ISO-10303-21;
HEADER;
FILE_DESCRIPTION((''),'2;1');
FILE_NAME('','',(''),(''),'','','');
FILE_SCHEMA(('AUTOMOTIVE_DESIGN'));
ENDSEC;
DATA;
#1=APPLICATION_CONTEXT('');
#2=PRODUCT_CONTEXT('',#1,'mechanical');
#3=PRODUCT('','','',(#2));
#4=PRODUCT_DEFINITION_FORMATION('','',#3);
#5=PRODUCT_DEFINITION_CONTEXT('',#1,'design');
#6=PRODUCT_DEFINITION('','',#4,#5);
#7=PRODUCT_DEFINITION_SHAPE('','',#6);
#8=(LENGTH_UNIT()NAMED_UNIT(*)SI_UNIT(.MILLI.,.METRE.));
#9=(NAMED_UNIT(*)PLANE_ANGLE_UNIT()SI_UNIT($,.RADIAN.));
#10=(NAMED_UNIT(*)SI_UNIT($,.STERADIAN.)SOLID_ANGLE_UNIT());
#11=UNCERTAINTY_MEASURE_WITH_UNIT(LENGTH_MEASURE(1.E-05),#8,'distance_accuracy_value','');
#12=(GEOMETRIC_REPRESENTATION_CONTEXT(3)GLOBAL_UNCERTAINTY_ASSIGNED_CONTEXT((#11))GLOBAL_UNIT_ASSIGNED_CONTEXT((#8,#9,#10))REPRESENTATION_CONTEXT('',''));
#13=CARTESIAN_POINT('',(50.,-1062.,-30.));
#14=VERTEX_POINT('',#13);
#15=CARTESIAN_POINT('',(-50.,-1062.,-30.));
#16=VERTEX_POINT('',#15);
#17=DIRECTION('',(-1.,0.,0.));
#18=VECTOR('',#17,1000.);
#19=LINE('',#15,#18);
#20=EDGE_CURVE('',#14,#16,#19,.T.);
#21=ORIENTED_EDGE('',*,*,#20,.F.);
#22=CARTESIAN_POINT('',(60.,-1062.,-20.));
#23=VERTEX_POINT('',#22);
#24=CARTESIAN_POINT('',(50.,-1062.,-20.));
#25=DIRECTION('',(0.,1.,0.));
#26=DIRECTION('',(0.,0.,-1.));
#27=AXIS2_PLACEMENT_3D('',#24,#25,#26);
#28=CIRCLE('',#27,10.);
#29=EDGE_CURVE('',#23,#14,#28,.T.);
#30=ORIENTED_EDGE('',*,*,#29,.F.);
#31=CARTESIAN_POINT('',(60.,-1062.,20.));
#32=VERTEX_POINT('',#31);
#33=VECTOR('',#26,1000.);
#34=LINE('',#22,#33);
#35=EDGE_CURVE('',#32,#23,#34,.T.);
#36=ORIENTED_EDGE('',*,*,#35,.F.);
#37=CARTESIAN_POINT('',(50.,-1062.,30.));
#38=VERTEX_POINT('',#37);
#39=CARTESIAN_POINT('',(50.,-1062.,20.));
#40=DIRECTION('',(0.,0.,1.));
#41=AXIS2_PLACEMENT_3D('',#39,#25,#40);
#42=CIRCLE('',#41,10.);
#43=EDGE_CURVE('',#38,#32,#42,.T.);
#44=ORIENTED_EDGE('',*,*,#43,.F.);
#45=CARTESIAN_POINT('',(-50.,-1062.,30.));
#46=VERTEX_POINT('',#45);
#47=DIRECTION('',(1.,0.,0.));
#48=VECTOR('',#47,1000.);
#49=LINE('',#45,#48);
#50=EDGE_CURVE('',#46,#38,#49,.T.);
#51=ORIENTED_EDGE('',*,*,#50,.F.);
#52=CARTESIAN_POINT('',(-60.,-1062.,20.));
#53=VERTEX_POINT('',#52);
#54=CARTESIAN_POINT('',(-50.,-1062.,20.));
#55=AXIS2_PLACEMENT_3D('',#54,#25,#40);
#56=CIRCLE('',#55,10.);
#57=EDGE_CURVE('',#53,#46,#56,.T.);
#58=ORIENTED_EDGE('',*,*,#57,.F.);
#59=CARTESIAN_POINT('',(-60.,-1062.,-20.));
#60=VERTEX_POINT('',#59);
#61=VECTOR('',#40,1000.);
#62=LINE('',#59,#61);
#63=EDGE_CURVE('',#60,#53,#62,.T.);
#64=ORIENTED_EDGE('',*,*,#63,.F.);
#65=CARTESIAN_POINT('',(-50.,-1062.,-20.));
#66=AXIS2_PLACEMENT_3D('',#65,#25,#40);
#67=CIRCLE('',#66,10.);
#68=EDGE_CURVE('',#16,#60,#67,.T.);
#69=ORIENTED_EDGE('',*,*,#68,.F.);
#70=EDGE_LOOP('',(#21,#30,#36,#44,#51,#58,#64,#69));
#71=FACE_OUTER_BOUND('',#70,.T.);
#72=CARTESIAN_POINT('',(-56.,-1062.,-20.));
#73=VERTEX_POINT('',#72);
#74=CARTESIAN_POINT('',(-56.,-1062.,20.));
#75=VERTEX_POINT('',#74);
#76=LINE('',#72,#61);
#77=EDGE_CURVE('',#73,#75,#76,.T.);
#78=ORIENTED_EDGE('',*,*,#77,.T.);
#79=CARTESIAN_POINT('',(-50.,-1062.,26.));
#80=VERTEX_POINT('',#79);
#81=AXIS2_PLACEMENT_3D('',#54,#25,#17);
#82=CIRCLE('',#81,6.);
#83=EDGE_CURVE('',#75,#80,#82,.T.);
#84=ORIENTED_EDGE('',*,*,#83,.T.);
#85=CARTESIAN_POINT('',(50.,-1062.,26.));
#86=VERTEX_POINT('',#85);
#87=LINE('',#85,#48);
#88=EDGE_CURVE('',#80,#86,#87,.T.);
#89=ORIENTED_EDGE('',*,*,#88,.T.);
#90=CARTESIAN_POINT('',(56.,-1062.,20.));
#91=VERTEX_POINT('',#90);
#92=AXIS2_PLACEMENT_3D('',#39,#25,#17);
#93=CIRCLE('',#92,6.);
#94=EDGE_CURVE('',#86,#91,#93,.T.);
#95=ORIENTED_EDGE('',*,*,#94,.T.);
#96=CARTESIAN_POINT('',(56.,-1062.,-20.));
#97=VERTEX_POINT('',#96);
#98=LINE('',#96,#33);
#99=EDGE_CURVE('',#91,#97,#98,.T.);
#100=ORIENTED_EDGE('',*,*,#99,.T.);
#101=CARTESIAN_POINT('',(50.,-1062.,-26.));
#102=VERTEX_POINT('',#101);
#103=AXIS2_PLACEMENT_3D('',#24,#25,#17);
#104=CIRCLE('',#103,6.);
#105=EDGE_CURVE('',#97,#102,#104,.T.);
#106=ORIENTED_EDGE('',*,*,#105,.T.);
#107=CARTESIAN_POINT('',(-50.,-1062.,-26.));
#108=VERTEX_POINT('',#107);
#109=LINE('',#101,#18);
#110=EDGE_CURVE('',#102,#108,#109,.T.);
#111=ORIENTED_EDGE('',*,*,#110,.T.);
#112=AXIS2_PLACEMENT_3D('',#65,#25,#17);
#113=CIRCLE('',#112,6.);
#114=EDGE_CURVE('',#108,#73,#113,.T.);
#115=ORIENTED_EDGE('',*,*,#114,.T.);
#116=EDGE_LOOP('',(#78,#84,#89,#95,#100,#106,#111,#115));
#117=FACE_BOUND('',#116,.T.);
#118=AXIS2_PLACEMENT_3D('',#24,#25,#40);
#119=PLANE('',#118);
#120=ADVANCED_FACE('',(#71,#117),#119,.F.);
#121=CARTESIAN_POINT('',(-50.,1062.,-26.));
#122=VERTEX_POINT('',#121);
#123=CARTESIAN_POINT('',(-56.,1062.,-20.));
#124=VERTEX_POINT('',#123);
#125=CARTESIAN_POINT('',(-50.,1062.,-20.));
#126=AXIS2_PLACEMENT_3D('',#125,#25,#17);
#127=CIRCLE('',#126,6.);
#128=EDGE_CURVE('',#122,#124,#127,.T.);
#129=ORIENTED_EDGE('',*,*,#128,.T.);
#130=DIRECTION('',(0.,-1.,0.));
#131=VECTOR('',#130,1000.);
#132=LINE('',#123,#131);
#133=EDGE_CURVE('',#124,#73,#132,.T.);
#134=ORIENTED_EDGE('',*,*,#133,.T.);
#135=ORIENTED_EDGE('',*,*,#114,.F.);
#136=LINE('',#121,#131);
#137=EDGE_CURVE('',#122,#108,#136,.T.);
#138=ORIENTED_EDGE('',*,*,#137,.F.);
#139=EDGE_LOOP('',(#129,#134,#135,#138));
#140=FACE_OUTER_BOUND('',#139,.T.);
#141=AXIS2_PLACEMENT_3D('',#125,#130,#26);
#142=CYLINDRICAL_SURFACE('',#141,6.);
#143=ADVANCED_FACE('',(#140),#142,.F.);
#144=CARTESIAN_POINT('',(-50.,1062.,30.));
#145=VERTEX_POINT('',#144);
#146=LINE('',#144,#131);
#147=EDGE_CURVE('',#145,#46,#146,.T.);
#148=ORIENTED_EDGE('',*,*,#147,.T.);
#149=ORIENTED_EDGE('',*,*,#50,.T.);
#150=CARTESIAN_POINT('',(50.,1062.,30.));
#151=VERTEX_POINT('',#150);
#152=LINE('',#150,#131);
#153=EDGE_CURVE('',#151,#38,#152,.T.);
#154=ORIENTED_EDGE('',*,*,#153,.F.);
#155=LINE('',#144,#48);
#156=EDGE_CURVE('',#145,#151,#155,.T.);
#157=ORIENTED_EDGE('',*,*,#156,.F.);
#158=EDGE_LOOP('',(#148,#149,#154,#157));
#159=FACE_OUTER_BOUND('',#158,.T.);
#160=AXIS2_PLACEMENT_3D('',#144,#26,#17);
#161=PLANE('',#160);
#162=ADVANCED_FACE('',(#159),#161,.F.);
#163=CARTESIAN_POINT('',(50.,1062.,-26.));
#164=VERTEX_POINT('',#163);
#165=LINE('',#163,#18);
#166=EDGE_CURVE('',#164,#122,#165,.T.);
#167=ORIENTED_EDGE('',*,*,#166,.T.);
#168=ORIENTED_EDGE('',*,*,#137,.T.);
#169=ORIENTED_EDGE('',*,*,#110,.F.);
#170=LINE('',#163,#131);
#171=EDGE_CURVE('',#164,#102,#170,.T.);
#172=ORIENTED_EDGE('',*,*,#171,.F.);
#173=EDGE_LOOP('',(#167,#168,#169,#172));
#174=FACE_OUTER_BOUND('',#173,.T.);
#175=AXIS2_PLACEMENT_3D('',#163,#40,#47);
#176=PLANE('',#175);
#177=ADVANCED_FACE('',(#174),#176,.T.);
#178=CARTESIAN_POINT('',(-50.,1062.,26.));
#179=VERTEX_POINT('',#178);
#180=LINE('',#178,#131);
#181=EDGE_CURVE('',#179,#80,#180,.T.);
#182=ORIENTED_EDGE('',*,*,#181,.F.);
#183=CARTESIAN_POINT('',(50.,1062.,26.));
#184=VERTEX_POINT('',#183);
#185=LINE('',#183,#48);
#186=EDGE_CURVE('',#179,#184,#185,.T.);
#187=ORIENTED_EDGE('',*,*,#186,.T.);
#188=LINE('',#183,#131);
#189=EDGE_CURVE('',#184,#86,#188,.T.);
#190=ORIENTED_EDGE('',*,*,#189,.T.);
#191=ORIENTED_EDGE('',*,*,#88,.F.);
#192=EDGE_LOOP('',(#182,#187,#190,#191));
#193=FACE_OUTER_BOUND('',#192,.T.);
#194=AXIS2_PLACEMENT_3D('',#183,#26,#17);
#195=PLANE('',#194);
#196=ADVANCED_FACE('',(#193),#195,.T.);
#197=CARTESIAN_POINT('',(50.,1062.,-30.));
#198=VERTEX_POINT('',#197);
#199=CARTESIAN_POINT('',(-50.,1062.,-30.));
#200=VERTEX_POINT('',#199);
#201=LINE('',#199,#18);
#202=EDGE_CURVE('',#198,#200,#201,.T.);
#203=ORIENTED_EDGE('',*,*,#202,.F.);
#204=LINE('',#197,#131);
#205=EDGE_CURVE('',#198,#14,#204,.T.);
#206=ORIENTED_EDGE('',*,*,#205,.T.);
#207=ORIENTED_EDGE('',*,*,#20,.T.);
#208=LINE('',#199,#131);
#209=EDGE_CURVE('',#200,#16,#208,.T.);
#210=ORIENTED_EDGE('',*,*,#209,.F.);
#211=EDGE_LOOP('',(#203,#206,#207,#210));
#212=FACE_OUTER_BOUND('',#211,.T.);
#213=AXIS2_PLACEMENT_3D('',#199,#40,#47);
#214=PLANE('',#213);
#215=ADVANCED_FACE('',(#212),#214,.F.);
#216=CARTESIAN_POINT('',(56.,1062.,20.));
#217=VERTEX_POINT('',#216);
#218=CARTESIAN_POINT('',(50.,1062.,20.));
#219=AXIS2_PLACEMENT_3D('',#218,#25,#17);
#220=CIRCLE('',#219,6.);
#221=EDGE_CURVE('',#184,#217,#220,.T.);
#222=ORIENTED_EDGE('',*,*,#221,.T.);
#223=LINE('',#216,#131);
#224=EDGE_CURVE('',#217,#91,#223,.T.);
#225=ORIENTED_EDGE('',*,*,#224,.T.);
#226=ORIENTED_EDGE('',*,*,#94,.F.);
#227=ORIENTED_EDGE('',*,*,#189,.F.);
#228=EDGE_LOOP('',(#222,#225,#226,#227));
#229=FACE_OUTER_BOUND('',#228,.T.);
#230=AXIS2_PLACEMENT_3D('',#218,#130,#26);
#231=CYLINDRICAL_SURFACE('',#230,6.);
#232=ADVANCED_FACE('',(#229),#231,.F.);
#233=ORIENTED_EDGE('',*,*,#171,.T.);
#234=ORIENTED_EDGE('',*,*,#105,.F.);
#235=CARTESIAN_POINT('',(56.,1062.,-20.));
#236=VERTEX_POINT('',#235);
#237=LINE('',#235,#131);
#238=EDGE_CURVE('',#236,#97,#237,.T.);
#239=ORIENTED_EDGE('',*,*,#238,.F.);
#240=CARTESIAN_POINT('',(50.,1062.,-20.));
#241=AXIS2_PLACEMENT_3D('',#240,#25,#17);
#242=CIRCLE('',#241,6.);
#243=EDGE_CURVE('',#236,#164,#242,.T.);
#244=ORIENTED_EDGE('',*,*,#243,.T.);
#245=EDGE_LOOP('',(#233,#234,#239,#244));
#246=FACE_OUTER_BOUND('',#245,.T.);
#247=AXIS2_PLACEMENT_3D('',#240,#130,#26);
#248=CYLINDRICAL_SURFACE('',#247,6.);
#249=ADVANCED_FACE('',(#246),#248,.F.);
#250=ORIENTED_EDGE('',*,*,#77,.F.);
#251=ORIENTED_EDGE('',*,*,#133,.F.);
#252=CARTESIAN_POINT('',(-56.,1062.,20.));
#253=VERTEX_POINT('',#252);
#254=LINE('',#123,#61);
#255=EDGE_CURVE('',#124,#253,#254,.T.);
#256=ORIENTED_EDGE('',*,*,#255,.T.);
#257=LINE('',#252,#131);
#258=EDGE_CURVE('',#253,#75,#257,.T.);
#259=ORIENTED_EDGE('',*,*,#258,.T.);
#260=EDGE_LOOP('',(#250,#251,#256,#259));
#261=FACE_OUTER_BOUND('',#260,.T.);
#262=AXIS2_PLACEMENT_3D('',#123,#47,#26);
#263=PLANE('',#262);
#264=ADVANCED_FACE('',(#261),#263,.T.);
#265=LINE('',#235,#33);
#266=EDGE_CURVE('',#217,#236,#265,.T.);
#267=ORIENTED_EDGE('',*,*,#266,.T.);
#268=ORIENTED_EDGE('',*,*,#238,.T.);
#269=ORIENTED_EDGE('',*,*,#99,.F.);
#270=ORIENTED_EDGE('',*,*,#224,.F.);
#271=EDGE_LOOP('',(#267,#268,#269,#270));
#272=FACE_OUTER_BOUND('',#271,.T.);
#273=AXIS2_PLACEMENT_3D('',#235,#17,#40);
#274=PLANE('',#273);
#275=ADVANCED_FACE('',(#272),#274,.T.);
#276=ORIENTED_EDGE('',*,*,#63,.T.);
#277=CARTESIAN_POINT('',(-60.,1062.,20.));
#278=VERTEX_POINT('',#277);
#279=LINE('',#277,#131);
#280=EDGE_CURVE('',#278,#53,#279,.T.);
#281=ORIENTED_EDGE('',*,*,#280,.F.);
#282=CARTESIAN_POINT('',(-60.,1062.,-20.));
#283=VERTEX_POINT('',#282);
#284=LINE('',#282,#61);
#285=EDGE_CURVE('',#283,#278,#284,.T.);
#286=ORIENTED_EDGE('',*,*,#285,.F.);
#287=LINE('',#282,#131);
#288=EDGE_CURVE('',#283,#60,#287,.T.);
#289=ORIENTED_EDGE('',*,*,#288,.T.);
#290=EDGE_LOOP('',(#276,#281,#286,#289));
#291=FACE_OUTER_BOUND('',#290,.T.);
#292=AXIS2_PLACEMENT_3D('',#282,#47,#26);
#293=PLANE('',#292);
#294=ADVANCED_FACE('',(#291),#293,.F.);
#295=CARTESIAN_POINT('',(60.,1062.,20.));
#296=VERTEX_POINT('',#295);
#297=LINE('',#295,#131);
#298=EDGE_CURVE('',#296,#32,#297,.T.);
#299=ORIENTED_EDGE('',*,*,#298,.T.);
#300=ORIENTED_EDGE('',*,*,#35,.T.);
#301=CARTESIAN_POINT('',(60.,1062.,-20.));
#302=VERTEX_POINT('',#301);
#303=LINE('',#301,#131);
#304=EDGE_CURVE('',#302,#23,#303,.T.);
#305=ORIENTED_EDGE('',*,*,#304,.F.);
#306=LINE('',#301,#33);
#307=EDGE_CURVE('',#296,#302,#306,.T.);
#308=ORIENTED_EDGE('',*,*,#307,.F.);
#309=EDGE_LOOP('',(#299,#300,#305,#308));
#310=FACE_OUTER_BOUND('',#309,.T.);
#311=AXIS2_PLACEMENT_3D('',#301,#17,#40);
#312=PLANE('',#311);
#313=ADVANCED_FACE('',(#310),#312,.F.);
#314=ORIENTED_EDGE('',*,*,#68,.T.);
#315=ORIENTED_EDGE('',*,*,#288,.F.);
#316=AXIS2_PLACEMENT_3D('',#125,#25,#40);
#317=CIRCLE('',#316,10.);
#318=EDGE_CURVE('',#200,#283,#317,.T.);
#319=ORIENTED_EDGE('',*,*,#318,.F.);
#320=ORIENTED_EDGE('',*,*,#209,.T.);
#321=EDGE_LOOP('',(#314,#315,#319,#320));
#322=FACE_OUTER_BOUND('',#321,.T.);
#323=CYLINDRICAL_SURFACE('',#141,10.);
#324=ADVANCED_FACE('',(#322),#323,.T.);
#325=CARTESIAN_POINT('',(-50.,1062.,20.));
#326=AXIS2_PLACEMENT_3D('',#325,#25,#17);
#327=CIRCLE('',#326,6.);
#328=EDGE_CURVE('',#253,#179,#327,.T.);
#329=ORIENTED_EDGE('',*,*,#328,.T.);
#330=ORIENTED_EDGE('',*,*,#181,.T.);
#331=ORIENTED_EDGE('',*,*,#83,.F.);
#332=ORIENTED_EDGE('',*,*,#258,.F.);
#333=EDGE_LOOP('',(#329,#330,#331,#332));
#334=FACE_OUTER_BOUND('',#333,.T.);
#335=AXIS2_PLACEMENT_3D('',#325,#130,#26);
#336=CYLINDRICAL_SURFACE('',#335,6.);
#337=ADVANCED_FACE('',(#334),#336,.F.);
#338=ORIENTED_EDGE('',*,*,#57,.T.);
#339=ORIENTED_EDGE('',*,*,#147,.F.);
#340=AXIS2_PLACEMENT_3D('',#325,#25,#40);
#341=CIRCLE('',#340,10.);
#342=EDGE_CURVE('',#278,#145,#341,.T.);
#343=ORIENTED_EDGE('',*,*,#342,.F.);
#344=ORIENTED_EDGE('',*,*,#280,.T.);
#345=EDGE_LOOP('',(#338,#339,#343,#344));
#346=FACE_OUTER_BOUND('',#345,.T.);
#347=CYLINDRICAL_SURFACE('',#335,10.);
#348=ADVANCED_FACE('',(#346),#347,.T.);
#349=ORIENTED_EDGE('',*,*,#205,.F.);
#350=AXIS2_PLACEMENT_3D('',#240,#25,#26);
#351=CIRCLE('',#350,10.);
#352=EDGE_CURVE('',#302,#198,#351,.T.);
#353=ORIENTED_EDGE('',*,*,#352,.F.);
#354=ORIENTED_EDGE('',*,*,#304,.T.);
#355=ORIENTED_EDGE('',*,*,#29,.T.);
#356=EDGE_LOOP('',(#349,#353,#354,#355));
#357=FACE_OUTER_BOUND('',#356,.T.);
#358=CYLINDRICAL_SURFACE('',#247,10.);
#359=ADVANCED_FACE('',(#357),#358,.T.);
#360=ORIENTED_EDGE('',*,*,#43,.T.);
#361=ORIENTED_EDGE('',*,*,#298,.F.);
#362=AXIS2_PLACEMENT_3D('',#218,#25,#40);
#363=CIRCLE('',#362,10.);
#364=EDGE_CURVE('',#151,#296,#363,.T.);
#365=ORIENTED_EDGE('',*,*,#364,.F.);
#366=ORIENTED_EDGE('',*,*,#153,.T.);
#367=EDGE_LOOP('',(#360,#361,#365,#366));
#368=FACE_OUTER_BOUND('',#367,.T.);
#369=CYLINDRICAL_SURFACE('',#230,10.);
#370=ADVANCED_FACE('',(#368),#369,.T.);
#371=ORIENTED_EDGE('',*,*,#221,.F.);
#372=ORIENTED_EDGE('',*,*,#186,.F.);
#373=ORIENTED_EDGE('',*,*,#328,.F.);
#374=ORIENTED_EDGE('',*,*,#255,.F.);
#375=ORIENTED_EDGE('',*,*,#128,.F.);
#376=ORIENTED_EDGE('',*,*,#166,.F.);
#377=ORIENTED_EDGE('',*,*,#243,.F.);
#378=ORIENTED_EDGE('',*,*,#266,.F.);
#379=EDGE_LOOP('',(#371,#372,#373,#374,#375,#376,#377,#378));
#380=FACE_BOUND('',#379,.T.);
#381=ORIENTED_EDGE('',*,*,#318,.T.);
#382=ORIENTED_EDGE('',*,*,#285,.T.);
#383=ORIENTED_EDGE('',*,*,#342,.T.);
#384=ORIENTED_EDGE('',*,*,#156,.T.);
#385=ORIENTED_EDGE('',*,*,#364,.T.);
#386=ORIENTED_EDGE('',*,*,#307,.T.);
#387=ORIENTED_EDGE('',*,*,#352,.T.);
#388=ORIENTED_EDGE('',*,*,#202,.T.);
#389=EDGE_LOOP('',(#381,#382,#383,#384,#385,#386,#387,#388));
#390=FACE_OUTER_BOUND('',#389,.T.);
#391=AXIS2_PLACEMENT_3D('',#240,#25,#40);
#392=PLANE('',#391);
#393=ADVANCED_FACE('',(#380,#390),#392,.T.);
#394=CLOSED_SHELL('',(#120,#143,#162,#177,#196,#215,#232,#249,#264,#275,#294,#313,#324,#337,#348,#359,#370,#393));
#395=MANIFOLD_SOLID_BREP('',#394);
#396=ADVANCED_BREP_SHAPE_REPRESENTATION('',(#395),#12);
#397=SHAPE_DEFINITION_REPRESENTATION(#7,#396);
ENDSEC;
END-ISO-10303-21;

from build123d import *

# Parameters (mm, degrees)
EXTRUDE_THIN1_DEPTH = 1062


with BuildPart() as part:
    # Sketch1 → Extrude-Thin1 (new, symmetric)
    with BuildSketch(Plane(origin=(0, 0, 0), x_dir=(1, 0, 0), z_dir=(0, 1, 0))):
        with BuildLine():
            Line((-50, 30), (50, 30))
            ThreePointArc((50, 30), (57.071067812, 27.071067812), (60, 20))
            Line((60, 20), (60, -20))
            ThreePointArc((60, -20), (57.071067812, -27.071067812), (50, -30))
            Line((50, -30), (-50, -30))
            ThreePointArc((-50, -30), (-57.071067812, -27.071067812), (-60, -20))
            Line((-60, -20), (-60, 20))
            ThreePointArc((-60, 20), (-57.071067812, 27.071067812), (-50, 30))
        make_face()
        with BuildLine():
            Line((-50, 26), (50, 26))
            ThreePointArc((50, 26), (54.242640687, 24.242640687), (56, 20))
            Line((56, 20), (56, -20))
            ThreePointArc((56, -20), (54.242640687, -24.242640687), (50, -26))
            Line((50, -26), (-50, -26))
            ThreePointArc((-50, -26), (-54.242640687, -24.242640687), (-56, -20))
            Line((-56, -20), (-56, 20))
            ThreePointArc((-56, 20), (-54.242640687, 24.242640687), (-50, 26))
        make_face(mode=Mode.SUBTRACT)
    extrude(amount=EXTRUDE_THIN1_DEPTH, both=True)


solid = part.part
